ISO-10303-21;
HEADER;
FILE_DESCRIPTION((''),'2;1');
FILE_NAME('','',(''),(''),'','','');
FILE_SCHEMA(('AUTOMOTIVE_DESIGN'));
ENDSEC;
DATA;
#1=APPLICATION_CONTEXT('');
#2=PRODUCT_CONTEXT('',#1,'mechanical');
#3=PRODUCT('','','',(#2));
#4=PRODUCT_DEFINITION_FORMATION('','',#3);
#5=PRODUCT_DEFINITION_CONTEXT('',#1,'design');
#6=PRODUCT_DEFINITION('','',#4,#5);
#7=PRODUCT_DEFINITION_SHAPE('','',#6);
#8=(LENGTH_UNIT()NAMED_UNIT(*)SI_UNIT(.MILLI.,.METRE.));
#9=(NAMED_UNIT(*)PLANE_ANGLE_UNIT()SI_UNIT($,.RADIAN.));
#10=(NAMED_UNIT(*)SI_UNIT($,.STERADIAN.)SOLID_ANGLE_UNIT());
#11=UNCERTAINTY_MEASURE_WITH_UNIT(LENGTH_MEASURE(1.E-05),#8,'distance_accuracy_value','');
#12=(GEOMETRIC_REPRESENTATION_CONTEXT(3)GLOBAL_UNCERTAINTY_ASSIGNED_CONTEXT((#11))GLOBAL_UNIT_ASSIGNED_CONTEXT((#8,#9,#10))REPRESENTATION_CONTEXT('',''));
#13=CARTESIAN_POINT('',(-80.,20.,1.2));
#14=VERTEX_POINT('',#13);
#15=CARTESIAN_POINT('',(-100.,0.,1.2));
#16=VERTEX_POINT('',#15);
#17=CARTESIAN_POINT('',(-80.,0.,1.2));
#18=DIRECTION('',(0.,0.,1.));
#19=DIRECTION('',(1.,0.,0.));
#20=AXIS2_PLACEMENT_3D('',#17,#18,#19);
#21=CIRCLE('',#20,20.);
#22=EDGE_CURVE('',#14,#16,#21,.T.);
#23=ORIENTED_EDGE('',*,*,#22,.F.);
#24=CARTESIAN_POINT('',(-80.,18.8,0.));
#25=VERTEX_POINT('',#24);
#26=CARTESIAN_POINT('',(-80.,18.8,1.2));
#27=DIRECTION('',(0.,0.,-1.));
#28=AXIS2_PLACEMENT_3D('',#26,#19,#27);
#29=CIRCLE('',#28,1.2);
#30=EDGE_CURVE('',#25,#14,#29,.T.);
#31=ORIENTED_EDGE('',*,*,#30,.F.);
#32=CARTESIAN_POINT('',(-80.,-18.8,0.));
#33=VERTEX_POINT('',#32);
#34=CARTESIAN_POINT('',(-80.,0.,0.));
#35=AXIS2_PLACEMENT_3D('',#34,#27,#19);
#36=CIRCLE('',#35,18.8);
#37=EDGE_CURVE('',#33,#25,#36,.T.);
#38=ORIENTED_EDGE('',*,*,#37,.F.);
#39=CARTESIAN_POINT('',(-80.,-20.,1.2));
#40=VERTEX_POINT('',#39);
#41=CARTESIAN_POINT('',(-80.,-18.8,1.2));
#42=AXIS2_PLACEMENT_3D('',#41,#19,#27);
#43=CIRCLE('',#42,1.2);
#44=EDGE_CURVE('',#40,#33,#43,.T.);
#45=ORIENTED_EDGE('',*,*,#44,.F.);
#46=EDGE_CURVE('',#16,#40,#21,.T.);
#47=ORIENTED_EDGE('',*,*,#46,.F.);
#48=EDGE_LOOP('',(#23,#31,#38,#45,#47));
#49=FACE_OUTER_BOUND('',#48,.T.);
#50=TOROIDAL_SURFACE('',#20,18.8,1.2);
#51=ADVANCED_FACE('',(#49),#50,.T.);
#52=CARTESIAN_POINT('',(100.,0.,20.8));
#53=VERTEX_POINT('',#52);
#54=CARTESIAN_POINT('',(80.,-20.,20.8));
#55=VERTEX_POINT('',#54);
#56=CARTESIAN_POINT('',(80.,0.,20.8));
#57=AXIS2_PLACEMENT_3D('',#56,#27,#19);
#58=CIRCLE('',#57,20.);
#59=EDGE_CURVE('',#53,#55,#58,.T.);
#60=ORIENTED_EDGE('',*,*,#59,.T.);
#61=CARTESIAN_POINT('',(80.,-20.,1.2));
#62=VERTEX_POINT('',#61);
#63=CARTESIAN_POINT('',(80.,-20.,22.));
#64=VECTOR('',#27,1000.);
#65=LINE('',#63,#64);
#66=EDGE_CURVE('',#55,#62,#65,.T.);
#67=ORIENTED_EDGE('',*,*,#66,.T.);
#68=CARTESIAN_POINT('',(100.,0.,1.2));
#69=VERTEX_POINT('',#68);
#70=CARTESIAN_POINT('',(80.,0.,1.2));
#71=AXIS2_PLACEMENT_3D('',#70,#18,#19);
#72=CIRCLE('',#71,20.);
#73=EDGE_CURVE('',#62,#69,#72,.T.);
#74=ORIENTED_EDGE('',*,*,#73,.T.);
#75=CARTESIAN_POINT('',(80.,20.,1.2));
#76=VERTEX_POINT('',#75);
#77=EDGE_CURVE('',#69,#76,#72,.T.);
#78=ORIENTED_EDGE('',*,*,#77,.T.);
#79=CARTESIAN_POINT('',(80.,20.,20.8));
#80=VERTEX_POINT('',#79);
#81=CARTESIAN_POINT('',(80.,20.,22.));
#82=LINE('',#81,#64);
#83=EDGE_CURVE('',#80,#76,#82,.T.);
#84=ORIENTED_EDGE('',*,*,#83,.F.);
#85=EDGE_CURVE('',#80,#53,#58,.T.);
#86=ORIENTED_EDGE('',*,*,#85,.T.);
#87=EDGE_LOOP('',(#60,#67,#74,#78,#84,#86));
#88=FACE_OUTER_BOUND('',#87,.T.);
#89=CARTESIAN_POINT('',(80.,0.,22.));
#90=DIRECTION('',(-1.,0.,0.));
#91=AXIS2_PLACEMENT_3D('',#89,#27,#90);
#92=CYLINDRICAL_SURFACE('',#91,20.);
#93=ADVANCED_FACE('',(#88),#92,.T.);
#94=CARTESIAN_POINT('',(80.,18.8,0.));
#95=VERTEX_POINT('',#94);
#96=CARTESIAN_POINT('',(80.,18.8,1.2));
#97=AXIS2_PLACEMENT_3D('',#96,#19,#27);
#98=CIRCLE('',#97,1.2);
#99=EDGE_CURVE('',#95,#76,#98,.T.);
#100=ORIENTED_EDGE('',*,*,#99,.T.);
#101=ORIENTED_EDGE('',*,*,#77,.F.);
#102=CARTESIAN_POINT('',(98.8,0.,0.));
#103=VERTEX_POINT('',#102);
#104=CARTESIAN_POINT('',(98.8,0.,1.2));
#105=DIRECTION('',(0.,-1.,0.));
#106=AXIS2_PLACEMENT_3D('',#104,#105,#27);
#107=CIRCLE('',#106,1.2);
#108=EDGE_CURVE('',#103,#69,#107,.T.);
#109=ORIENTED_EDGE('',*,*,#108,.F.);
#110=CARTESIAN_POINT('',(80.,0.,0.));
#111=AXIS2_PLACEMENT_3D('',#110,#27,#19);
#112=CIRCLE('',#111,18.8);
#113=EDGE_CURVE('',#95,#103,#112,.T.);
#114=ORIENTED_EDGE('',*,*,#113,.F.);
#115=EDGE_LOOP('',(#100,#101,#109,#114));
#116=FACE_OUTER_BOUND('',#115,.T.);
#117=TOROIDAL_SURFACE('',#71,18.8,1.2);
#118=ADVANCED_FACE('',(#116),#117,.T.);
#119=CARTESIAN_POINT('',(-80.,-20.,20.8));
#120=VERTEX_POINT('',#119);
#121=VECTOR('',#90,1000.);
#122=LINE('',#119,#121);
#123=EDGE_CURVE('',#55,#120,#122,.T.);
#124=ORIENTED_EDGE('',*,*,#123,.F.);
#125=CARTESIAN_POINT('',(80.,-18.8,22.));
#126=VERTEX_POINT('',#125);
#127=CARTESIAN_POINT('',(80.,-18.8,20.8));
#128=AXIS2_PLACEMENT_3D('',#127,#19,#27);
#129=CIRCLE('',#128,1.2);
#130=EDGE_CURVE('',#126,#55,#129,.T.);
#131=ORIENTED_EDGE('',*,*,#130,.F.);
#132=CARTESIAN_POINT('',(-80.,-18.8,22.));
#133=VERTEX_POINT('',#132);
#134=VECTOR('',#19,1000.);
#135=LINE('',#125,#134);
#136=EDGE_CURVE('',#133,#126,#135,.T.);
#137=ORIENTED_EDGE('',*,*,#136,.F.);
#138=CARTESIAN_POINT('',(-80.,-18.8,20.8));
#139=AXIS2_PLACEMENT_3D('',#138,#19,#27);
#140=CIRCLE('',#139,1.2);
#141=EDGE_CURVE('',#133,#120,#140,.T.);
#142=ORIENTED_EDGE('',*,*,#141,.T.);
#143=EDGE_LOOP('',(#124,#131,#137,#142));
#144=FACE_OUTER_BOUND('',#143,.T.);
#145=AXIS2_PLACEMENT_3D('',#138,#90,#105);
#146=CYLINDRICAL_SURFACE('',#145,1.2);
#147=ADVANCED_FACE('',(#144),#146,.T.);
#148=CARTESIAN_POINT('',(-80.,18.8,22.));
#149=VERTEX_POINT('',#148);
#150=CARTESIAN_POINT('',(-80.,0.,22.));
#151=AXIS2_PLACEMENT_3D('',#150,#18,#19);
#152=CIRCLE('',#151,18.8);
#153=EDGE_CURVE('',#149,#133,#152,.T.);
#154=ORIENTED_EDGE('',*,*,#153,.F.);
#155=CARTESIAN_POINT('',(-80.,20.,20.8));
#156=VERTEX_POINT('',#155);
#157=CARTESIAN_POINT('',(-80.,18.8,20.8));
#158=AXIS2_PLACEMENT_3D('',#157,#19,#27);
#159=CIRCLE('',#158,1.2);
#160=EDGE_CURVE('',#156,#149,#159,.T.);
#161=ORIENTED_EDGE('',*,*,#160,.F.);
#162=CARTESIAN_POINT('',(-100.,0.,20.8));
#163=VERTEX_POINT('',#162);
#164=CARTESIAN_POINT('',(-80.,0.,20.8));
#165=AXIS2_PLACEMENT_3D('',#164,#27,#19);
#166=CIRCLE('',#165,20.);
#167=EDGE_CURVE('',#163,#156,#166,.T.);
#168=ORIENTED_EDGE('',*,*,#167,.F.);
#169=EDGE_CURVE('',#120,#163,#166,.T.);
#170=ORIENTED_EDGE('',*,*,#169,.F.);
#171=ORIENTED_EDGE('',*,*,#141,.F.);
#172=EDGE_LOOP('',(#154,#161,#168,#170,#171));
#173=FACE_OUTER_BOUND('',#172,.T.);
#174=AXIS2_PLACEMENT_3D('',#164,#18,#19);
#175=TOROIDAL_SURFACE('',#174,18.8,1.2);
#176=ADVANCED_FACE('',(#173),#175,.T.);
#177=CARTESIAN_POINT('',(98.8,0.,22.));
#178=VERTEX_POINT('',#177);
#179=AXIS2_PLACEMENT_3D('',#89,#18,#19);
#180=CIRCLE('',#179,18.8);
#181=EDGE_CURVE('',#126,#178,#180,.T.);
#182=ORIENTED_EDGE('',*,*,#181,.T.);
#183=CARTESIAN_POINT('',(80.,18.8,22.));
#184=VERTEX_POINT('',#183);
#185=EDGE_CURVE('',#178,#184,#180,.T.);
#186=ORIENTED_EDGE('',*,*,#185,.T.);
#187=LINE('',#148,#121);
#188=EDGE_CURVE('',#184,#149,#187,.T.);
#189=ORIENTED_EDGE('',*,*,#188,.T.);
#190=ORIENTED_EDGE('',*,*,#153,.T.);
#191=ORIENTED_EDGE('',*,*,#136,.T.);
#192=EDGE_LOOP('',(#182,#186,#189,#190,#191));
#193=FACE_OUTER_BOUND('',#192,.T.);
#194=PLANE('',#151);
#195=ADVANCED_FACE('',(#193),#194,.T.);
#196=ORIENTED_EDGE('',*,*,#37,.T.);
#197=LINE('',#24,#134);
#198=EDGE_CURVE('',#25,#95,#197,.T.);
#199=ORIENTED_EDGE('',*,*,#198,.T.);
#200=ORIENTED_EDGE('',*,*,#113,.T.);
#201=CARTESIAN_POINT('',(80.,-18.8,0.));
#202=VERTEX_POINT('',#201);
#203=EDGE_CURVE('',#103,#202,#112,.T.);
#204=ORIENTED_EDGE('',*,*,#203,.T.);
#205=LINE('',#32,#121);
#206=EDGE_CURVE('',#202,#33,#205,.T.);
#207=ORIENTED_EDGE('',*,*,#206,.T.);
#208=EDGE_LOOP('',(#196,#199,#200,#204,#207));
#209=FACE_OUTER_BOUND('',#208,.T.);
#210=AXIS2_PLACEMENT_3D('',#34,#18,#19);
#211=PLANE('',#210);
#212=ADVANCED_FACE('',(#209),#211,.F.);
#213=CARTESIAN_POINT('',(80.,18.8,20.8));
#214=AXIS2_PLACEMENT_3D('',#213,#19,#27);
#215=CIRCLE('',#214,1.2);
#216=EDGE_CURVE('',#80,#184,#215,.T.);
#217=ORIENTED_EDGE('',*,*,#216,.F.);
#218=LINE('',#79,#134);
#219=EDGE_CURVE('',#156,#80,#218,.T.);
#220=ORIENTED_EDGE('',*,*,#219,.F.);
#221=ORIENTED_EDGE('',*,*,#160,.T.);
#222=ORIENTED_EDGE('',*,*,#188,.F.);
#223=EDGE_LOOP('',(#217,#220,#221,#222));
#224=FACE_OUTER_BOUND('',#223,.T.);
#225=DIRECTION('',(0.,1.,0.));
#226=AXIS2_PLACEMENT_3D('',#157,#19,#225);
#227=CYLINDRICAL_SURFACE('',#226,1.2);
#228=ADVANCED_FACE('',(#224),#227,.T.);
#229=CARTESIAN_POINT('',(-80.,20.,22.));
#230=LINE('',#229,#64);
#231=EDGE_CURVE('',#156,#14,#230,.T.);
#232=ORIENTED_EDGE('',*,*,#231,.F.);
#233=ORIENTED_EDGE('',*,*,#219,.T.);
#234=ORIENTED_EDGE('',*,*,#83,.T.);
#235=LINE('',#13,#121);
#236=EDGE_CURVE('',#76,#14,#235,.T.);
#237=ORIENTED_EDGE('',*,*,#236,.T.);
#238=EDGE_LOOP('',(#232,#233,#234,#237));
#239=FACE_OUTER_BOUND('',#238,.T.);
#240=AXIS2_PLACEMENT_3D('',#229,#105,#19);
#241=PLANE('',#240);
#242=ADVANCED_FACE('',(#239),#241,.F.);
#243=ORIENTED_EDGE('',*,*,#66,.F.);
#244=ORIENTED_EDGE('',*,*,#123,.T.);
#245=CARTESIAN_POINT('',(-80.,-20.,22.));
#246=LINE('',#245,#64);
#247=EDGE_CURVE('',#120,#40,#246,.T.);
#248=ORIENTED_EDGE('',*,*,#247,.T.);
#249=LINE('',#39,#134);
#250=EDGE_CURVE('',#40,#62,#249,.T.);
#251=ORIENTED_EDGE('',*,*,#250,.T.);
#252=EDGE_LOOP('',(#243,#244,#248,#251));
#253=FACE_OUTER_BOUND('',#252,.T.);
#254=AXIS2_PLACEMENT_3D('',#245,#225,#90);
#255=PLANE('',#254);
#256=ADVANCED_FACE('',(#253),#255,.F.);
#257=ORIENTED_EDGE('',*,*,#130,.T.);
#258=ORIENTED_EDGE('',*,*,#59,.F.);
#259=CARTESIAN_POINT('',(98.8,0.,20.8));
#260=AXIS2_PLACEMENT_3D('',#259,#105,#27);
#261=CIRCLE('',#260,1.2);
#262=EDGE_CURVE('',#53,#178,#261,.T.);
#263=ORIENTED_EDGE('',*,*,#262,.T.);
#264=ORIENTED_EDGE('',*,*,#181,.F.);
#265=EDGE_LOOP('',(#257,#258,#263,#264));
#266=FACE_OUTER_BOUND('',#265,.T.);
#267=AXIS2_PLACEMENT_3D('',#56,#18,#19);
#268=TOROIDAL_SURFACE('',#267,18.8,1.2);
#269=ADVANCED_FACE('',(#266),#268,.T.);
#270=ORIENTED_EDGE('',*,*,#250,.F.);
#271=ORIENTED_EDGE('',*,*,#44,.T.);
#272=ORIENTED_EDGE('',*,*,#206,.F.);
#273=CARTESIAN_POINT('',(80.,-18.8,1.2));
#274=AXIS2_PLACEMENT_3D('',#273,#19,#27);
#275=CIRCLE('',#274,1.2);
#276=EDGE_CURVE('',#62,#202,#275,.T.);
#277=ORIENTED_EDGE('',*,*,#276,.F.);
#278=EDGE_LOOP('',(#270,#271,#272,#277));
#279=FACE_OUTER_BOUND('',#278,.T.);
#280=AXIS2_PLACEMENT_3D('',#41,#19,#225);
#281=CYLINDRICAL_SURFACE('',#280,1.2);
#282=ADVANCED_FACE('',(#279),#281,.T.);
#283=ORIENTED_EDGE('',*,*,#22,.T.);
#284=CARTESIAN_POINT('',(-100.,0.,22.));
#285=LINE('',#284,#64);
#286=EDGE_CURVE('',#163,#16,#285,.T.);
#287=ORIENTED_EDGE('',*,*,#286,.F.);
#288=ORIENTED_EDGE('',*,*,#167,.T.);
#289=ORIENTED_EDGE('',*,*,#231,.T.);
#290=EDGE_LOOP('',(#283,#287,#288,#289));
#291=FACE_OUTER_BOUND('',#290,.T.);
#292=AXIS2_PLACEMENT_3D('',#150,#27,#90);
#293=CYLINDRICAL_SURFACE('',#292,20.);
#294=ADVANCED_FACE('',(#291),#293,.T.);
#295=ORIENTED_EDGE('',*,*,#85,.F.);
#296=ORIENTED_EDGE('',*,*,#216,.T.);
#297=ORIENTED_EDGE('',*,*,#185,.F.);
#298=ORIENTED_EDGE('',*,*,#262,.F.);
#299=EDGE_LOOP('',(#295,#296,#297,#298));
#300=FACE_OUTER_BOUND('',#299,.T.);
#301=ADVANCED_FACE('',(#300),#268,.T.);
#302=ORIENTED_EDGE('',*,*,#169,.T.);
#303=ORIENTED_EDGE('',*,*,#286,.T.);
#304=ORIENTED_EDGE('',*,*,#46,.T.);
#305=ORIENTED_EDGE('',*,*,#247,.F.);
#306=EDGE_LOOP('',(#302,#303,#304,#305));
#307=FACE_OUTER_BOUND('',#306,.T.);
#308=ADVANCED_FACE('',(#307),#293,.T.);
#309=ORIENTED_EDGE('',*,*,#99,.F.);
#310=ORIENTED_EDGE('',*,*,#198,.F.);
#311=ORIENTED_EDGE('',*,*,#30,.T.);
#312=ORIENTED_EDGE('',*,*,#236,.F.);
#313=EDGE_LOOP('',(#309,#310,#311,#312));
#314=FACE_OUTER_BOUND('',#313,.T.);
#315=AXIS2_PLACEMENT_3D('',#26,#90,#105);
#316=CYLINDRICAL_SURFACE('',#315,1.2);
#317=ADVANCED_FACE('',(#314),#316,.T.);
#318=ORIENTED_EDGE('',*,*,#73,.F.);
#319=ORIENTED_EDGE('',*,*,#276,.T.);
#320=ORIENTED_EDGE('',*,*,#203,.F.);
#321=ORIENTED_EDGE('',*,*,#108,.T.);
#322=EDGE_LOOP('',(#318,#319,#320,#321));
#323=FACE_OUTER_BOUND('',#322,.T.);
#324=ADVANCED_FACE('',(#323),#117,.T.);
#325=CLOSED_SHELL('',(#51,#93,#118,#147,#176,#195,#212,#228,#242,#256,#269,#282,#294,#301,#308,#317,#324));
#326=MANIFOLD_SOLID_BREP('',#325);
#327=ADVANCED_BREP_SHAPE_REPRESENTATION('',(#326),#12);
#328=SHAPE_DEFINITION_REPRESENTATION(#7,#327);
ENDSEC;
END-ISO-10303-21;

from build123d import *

# Parameters (mm, degrees)
BASE_EXTRUDE_DEPTH = 22
FILLET1_R          = 1.2


with BuildPart() as part:
    # Sketch1 → Base-Extrude (new body)
    with BuildSketch(Plane.XY):
        with BuildLine():
            Line((-80, 20), (80, 20))
            ThreePointArc((80, 20), (100, 0), (80, -20))
            Line((80, -20), (-80, -20))
            ThreePointArc((-80, -20), (-100, 0), (-80, 20))
        make_face()
    extrude(amount=BASE_EXTRUDE_DEPTH)

    # Fillet1
    fillet1_edges = [part.edges().sort_by_distance(p)[0] for p in [
        (100, 0, 22),
        (0, 20, 22),
        (-100, 0, 22),
        (0, 20, 0),
        (100, 0, 0),
        (0, -20, 0),
        (-100, 0, 0),
        (0, -20, 22),
    ]]
    fillet(fillet1_edges, radius=FILLET1_R)


solid = part.part
